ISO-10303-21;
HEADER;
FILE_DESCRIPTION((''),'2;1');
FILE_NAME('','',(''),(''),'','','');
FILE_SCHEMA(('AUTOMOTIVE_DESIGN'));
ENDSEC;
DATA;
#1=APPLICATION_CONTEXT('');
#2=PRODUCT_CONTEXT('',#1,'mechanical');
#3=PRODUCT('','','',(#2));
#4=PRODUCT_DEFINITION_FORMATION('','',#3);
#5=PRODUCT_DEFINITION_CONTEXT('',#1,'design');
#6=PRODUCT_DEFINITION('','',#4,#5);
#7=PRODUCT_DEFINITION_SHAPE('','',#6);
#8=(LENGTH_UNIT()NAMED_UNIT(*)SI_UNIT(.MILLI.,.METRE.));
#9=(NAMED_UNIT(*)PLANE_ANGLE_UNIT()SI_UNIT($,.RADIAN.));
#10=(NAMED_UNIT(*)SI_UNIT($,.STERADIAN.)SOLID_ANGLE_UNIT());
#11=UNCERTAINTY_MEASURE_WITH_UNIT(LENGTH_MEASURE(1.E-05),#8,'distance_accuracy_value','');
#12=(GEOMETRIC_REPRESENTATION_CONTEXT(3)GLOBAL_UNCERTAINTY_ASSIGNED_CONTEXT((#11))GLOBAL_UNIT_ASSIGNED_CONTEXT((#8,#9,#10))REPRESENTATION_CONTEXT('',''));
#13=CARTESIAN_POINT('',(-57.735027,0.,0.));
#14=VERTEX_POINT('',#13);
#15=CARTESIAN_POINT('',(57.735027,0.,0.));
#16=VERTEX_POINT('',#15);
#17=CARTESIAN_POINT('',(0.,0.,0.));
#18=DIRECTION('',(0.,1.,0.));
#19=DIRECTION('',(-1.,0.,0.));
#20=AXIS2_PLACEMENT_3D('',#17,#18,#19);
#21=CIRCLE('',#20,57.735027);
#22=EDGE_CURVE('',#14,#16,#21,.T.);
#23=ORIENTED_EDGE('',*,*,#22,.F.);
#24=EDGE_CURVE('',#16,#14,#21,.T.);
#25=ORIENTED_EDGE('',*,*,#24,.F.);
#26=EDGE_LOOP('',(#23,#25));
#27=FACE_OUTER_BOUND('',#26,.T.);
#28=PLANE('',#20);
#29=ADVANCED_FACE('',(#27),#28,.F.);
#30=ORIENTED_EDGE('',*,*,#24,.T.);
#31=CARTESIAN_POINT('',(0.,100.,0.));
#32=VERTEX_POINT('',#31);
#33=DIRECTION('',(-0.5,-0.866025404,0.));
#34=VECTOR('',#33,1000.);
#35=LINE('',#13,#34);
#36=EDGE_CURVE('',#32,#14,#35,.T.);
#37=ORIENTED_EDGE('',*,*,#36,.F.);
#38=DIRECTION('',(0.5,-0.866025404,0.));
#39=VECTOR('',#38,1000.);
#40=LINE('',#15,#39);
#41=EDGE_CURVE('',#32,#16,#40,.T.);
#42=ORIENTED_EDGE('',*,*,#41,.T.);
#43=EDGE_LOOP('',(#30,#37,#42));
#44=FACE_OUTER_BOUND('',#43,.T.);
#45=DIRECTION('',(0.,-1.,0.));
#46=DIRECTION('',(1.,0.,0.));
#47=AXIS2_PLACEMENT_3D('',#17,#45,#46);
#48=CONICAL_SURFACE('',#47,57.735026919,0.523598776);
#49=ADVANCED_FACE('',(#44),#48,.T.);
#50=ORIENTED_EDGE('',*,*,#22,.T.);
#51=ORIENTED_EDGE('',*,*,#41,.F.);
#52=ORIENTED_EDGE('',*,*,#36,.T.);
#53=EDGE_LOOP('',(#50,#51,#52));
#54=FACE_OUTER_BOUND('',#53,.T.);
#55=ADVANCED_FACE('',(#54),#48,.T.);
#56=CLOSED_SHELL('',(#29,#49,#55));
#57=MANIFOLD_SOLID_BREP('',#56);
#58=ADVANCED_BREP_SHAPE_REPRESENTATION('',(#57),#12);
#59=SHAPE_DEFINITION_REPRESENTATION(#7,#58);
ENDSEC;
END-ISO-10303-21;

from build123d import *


with BuildPart() as part:
    # 草图1 → 旋转1 (revolve)
    with BuildSketch(Plane.XY):
        Polygon((0, 0), (57.735026919, 0), (0, 100), align=None)
    revolve(axis=Axis((0, 100, 0), (0, -1, 0)))


solid = part.part
